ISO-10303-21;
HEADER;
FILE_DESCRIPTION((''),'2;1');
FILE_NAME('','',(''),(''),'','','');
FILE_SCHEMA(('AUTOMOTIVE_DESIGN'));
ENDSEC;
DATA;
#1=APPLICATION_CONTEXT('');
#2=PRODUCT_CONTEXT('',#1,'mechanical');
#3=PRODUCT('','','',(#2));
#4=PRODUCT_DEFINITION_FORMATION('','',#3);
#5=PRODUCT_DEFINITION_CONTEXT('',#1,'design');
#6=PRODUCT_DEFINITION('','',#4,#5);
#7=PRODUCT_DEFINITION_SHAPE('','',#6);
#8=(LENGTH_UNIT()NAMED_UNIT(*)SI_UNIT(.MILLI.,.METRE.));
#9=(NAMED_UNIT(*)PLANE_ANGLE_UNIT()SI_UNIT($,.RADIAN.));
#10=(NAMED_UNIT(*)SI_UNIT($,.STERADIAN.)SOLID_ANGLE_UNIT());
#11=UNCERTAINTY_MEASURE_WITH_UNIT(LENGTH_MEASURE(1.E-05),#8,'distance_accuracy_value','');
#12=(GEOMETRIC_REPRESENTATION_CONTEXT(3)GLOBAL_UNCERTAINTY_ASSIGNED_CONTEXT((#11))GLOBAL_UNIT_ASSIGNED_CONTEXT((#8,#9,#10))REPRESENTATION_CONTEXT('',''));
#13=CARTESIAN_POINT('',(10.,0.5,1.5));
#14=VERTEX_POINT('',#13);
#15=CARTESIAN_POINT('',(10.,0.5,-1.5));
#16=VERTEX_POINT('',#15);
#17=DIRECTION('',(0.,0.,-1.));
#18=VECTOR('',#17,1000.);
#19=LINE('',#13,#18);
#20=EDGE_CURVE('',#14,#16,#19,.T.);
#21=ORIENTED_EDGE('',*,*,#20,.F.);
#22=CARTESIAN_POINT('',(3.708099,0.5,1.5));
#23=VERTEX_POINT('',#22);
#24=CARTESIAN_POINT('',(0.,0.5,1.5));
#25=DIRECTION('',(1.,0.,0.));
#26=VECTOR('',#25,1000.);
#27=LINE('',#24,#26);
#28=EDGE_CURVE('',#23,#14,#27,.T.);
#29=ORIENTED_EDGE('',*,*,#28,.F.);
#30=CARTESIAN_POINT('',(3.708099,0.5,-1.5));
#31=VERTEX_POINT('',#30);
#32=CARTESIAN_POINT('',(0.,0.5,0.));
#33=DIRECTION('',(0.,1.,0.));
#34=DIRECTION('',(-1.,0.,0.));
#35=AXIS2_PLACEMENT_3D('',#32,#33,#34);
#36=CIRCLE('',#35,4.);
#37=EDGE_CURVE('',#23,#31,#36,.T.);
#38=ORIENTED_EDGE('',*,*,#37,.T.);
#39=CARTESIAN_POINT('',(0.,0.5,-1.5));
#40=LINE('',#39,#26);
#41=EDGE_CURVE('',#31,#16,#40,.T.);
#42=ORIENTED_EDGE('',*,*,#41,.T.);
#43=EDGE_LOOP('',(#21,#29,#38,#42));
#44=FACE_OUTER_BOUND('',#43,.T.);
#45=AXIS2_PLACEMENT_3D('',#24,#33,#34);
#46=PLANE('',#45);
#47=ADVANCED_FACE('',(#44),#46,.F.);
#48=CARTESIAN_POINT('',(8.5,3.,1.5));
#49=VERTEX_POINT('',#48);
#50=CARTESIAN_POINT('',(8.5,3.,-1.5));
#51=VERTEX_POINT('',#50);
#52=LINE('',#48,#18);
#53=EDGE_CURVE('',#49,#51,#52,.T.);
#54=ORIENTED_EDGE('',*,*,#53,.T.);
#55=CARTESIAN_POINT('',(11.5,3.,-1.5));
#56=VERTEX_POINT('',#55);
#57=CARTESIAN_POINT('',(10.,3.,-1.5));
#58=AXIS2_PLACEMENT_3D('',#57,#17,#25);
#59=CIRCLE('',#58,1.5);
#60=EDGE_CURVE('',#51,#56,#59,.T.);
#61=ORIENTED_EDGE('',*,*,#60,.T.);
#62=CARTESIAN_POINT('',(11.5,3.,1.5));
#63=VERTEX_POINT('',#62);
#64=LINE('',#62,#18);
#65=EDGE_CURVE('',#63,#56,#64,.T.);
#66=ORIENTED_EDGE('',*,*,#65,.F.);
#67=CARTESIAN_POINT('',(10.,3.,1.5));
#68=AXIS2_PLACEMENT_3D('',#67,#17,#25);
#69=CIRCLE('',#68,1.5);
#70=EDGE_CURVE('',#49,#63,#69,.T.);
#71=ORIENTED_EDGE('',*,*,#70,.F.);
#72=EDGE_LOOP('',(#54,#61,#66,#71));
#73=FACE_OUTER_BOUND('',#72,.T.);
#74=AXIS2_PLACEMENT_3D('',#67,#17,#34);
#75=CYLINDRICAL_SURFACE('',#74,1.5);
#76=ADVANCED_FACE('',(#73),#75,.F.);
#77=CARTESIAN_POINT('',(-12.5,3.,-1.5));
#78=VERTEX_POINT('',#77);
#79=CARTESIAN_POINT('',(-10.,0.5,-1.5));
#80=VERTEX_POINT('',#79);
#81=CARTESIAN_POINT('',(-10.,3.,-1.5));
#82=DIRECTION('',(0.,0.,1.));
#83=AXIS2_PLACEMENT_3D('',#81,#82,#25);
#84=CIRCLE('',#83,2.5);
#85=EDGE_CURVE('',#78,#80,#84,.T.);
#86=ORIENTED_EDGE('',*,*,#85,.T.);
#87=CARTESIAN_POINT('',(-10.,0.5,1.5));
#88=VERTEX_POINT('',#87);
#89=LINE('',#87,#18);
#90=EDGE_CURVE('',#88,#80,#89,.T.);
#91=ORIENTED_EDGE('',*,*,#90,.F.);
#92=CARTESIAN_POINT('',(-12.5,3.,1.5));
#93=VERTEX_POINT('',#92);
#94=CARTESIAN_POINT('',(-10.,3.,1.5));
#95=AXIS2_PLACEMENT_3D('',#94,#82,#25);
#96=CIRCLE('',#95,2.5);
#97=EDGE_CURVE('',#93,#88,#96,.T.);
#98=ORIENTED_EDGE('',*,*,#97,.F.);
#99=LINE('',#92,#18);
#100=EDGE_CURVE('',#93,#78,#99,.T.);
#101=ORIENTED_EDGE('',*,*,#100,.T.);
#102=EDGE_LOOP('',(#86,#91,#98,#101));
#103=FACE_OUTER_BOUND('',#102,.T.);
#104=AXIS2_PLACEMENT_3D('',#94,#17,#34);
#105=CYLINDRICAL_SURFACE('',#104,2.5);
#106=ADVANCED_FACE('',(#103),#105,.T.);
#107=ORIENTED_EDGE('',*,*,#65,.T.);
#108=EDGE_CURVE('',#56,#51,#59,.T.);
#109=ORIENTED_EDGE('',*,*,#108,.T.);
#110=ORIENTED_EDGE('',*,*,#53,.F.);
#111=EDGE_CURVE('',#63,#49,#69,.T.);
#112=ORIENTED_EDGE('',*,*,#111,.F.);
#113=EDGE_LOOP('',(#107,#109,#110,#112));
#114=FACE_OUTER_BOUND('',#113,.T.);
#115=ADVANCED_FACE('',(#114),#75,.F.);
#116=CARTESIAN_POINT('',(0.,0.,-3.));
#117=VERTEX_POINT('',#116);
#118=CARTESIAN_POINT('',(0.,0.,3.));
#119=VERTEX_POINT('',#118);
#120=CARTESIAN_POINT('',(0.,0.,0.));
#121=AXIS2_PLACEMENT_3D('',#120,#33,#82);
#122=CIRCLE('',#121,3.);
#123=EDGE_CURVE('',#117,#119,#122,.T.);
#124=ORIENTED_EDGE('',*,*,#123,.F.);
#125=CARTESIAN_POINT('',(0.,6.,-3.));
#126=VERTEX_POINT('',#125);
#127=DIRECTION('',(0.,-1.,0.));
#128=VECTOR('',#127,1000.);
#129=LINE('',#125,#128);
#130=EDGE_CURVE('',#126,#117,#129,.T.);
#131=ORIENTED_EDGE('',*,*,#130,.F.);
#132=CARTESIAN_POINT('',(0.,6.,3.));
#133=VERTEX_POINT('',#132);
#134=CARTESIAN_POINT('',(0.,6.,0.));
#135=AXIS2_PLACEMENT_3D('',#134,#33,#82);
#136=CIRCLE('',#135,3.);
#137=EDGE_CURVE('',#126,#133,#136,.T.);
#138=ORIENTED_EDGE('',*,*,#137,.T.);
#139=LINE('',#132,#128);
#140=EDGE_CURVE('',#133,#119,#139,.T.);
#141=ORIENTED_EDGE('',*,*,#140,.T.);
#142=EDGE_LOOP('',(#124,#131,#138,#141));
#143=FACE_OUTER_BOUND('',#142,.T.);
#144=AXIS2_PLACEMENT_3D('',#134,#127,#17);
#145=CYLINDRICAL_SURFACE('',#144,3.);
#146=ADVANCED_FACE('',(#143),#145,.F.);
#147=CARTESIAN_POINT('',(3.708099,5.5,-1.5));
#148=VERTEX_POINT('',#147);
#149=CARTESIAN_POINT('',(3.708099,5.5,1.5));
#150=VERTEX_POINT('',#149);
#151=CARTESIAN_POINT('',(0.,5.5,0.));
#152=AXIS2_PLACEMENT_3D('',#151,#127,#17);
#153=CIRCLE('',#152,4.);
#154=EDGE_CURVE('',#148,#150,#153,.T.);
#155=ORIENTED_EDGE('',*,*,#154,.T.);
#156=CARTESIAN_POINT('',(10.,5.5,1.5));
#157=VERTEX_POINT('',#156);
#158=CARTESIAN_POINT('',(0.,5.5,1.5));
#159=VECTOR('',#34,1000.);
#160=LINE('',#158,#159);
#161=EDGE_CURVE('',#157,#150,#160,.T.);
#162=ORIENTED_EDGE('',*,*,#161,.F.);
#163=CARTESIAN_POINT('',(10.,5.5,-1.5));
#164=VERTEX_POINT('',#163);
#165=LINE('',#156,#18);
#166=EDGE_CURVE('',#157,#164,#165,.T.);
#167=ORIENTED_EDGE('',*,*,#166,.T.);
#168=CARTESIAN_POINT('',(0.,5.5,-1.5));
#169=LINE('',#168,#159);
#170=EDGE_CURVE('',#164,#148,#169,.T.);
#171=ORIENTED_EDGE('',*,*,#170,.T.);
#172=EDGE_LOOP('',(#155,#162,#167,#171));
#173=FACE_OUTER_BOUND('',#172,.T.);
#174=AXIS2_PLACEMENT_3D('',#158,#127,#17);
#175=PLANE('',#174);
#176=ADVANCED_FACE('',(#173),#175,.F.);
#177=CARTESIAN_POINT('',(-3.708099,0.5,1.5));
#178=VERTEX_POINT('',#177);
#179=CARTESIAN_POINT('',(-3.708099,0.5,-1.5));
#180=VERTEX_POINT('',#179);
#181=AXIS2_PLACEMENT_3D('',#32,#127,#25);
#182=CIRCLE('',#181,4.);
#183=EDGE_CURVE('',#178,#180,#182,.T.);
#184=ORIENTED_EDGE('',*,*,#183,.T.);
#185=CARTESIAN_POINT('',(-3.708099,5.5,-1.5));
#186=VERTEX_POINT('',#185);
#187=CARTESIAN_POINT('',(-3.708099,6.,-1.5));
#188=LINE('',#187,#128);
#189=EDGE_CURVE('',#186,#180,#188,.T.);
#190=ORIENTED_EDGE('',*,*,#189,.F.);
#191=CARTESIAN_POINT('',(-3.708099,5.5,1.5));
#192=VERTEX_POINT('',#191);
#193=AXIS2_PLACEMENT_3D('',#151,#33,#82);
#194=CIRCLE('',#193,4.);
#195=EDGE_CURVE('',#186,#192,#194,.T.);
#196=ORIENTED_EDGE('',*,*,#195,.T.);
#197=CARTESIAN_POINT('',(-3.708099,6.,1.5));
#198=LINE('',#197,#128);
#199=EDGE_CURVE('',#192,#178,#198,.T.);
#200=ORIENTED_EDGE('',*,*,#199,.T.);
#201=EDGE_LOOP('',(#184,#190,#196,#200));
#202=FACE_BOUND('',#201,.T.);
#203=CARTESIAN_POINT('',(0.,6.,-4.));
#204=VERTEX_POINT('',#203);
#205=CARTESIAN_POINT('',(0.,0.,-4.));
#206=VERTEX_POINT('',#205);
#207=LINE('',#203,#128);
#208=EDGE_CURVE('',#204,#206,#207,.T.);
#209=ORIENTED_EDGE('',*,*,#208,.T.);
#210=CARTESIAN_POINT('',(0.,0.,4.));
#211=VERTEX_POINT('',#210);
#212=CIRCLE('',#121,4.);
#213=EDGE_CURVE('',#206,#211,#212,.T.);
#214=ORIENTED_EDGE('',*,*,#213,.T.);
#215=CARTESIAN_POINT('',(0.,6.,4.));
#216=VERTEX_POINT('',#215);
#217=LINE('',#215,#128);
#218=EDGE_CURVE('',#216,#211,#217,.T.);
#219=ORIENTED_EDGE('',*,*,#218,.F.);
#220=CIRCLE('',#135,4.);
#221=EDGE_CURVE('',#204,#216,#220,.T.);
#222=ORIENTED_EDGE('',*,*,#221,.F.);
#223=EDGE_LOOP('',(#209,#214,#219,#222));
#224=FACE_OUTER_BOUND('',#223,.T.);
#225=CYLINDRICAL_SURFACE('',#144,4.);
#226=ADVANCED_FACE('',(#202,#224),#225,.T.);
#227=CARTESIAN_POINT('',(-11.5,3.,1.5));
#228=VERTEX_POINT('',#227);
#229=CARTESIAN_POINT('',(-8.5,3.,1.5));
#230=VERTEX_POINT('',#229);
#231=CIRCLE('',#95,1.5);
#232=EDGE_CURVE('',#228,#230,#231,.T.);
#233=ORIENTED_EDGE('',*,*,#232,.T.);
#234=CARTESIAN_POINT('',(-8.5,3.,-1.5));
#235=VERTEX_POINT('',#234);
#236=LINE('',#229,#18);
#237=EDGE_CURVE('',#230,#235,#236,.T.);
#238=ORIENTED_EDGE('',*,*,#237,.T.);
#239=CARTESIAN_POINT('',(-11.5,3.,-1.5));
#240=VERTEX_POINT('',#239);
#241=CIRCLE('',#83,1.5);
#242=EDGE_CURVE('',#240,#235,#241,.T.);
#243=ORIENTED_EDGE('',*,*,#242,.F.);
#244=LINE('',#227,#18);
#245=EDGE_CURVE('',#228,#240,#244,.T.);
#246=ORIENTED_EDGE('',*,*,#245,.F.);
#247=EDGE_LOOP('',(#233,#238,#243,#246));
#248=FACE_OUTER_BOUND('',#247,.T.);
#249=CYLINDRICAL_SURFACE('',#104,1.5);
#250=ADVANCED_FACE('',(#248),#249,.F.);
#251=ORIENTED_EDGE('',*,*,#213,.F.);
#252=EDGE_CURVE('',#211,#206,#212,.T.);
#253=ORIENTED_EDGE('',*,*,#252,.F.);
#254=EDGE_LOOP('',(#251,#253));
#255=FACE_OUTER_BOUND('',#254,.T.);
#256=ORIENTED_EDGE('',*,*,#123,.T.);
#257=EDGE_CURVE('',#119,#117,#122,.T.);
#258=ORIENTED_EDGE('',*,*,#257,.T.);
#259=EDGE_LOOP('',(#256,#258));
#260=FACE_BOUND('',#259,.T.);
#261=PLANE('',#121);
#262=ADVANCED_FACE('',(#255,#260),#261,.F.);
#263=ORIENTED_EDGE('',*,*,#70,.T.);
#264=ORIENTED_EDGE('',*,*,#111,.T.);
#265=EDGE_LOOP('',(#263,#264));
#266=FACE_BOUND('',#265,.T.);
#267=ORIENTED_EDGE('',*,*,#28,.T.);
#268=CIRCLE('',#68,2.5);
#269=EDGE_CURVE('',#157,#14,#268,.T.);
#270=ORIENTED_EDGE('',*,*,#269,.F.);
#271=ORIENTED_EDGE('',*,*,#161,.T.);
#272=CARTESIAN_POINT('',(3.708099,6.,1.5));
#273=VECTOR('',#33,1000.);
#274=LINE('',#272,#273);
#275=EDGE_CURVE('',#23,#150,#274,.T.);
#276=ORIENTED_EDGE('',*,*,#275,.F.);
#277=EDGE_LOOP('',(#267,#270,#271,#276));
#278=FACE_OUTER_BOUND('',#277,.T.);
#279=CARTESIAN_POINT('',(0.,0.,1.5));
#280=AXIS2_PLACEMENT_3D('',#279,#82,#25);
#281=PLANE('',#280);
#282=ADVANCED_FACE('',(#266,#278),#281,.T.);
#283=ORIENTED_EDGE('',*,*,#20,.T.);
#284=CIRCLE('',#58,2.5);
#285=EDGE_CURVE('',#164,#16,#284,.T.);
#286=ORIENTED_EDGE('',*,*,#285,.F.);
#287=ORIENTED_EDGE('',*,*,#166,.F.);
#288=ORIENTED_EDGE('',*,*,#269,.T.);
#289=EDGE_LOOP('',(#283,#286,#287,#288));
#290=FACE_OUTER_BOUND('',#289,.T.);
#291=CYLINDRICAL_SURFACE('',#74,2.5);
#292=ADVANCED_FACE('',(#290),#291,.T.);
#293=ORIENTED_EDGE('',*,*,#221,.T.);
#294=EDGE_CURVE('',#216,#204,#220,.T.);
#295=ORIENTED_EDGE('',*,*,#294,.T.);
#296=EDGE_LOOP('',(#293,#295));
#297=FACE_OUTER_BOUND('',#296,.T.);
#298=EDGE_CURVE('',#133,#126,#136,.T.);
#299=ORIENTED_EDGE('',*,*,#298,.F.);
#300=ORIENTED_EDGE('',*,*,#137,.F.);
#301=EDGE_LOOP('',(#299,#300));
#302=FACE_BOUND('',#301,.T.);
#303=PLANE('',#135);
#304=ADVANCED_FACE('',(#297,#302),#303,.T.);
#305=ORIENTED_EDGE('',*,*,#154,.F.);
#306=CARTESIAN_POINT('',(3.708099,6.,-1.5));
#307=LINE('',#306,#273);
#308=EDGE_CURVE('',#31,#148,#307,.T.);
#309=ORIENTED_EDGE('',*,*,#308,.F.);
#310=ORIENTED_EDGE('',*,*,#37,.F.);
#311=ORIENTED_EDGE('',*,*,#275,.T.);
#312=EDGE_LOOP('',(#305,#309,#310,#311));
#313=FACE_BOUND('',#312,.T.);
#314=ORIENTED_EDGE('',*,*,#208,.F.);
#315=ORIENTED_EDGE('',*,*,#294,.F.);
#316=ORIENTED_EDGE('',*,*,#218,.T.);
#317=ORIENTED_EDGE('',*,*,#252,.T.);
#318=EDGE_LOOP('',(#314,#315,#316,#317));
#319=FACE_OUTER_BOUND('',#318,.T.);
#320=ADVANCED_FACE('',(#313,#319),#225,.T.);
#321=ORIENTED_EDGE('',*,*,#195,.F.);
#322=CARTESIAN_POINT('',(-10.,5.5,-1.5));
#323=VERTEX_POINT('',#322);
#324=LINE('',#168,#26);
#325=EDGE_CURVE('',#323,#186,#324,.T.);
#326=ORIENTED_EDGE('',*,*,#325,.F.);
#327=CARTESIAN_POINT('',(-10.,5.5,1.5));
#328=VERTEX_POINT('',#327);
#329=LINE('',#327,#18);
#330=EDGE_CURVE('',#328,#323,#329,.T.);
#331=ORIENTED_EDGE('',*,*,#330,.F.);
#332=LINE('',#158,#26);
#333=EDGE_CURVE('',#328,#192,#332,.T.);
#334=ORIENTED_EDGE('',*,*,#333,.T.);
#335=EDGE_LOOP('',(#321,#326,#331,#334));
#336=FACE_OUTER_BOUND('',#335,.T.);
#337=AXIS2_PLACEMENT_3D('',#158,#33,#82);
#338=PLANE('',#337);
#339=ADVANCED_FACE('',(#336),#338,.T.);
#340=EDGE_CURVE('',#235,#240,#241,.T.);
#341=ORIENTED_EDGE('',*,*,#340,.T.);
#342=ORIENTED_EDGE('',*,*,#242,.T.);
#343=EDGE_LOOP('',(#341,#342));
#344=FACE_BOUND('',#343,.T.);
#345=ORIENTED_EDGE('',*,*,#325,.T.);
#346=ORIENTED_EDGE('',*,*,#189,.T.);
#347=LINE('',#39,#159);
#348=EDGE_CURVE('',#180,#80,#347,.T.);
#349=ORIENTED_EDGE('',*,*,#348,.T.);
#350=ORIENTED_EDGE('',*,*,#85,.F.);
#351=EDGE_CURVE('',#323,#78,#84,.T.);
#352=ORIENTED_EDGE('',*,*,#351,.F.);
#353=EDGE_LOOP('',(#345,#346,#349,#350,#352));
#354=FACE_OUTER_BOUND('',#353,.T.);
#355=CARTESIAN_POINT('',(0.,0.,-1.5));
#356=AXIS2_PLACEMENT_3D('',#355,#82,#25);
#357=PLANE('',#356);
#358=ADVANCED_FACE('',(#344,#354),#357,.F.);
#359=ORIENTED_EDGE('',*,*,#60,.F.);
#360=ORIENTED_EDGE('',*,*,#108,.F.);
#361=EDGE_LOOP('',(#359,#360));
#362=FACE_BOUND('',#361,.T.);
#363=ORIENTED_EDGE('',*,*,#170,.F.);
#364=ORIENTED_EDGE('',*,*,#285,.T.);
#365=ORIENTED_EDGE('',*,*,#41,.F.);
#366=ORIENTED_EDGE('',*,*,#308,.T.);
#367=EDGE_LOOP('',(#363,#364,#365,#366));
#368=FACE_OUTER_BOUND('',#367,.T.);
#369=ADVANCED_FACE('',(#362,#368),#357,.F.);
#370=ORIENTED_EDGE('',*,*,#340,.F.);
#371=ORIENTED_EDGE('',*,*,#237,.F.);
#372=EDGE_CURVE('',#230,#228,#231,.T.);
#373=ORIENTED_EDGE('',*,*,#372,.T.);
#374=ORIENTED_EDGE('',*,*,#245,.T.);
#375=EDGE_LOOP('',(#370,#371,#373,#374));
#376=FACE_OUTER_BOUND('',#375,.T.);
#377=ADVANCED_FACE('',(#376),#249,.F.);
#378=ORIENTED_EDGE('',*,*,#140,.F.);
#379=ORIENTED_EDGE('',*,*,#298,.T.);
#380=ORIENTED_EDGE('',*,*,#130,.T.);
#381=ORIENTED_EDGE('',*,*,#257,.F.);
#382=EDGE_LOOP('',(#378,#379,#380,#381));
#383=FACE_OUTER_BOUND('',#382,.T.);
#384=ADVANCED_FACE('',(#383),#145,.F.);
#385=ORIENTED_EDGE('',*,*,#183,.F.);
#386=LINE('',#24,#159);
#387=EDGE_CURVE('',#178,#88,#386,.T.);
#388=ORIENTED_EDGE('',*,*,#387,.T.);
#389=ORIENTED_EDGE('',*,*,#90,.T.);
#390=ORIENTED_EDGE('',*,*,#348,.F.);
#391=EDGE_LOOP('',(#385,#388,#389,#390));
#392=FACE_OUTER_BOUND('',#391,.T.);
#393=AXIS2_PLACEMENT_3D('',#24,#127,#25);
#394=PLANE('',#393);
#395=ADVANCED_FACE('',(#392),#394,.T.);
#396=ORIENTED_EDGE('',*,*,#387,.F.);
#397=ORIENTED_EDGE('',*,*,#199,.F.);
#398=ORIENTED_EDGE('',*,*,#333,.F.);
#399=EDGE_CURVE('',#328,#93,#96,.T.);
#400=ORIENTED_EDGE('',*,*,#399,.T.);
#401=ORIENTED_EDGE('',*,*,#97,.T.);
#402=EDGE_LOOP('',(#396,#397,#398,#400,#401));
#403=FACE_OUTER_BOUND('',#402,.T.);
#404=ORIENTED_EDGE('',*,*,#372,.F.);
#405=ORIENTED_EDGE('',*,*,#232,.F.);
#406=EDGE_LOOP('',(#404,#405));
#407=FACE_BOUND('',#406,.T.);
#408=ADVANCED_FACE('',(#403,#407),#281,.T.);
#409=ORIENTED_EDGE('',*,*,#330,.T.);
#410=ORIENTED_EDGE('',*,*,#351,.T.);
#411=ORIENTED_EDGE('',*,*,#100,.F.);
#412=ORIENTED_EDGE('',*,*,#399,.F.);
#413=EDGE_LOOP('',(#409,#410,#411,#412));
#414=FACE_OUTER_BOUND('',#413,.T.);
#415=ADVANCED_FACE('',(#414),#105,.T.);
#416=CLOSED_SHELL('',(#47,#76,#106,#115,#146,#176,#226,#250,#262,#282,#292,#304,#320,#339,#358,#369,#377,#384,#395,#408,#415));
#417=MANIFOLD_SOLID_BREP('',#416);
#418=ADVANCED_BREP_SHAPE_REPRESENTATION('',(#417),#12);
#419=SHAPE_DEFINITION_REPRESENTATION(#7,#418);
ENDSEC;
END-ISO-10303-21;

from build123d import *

# Parameters (mm, degrees)
SKETCH1_R           = 4
SKETCH1_R_2         = 3
BOSS_EXTRUDE1_DEPTH = 6
SKETCH2_R           = 2.5
SKETCH2_R_2         = 1.5
BOSS_EXTRUDE2_DEPTH = 1.5


with BuildPart() as part:
    # Sketch1 → Boss-Extrude1 (new body)
    with BuildSketch(Plane(origin=(0, 0, 0), x_dir=(1, 0, 0), z_dir=(0, 1, 0))):
        with Locations(Location((0, 0, 0), (0, 0, 270))):
            Circle(SKETCH1_R)
        with Locations(Location((0, 0, 0), (0, 0, 270))):
            Circle(SKETCH1_R_2, mode=Mode.SUBTRACT)
    extrude(amount=BOSS_EXTRUDE1_DEPTH)

    # Sketch2 → Boss-Extrude2 (add, symmetric)
    # profile 1 of 4: a face of its own
    with BuildSketch(Plane.XY):
        with BuildLine():
            Line((-3, 5.5), (-10, 5.5))
            ThreePointArc((-10, 5.5), (-8.232233047, 4.767766953), (-7.5, 3))
            ThreePointArc((-7.5, 3), (-8.232233047, 1.232233047), (-10, 0.5))
            Line((-10, 0.5), (-3, 0.5))
            Line((-3, 0.5), (-3, 5.5))
        make_face()
    # profile 2 of 4: a face of its own
    with BuildSketch(Plane.XY):
        with Locations((-10, 3)):
            Circle(SKETCH2_R)
        with Locations((-10, 3)):
            Circle(SKETCH2_R_2, mode=Mode.SUBTRACT)
    # profile 3 of 4: a face of its own
    with BuildSketch(Plane.XY):
        with BuildLine():
            Line((3, 5.5), (3, 0.5))
            Line((3, 0.5), (10, 0.5))
            ThreePointArc((10, 0.5), (7.5, 3), (10, 5.5))
            Line((10, 5.5), (3, 5.5))
        make_face()
    # profile 4 of 4: a face of its own
    with BuildSketch(Plane.XY):
        with Locations((10, 3)):
            Circle(SKETCH2_R)
        with Locations((10, 3)):
            Circle(SKETCH2_R_2, mode=Mode.SUBTRACT)
    extrude(amount=BOSS_EXTRUDE2_DEPTH, both=True)


solid = part.part
